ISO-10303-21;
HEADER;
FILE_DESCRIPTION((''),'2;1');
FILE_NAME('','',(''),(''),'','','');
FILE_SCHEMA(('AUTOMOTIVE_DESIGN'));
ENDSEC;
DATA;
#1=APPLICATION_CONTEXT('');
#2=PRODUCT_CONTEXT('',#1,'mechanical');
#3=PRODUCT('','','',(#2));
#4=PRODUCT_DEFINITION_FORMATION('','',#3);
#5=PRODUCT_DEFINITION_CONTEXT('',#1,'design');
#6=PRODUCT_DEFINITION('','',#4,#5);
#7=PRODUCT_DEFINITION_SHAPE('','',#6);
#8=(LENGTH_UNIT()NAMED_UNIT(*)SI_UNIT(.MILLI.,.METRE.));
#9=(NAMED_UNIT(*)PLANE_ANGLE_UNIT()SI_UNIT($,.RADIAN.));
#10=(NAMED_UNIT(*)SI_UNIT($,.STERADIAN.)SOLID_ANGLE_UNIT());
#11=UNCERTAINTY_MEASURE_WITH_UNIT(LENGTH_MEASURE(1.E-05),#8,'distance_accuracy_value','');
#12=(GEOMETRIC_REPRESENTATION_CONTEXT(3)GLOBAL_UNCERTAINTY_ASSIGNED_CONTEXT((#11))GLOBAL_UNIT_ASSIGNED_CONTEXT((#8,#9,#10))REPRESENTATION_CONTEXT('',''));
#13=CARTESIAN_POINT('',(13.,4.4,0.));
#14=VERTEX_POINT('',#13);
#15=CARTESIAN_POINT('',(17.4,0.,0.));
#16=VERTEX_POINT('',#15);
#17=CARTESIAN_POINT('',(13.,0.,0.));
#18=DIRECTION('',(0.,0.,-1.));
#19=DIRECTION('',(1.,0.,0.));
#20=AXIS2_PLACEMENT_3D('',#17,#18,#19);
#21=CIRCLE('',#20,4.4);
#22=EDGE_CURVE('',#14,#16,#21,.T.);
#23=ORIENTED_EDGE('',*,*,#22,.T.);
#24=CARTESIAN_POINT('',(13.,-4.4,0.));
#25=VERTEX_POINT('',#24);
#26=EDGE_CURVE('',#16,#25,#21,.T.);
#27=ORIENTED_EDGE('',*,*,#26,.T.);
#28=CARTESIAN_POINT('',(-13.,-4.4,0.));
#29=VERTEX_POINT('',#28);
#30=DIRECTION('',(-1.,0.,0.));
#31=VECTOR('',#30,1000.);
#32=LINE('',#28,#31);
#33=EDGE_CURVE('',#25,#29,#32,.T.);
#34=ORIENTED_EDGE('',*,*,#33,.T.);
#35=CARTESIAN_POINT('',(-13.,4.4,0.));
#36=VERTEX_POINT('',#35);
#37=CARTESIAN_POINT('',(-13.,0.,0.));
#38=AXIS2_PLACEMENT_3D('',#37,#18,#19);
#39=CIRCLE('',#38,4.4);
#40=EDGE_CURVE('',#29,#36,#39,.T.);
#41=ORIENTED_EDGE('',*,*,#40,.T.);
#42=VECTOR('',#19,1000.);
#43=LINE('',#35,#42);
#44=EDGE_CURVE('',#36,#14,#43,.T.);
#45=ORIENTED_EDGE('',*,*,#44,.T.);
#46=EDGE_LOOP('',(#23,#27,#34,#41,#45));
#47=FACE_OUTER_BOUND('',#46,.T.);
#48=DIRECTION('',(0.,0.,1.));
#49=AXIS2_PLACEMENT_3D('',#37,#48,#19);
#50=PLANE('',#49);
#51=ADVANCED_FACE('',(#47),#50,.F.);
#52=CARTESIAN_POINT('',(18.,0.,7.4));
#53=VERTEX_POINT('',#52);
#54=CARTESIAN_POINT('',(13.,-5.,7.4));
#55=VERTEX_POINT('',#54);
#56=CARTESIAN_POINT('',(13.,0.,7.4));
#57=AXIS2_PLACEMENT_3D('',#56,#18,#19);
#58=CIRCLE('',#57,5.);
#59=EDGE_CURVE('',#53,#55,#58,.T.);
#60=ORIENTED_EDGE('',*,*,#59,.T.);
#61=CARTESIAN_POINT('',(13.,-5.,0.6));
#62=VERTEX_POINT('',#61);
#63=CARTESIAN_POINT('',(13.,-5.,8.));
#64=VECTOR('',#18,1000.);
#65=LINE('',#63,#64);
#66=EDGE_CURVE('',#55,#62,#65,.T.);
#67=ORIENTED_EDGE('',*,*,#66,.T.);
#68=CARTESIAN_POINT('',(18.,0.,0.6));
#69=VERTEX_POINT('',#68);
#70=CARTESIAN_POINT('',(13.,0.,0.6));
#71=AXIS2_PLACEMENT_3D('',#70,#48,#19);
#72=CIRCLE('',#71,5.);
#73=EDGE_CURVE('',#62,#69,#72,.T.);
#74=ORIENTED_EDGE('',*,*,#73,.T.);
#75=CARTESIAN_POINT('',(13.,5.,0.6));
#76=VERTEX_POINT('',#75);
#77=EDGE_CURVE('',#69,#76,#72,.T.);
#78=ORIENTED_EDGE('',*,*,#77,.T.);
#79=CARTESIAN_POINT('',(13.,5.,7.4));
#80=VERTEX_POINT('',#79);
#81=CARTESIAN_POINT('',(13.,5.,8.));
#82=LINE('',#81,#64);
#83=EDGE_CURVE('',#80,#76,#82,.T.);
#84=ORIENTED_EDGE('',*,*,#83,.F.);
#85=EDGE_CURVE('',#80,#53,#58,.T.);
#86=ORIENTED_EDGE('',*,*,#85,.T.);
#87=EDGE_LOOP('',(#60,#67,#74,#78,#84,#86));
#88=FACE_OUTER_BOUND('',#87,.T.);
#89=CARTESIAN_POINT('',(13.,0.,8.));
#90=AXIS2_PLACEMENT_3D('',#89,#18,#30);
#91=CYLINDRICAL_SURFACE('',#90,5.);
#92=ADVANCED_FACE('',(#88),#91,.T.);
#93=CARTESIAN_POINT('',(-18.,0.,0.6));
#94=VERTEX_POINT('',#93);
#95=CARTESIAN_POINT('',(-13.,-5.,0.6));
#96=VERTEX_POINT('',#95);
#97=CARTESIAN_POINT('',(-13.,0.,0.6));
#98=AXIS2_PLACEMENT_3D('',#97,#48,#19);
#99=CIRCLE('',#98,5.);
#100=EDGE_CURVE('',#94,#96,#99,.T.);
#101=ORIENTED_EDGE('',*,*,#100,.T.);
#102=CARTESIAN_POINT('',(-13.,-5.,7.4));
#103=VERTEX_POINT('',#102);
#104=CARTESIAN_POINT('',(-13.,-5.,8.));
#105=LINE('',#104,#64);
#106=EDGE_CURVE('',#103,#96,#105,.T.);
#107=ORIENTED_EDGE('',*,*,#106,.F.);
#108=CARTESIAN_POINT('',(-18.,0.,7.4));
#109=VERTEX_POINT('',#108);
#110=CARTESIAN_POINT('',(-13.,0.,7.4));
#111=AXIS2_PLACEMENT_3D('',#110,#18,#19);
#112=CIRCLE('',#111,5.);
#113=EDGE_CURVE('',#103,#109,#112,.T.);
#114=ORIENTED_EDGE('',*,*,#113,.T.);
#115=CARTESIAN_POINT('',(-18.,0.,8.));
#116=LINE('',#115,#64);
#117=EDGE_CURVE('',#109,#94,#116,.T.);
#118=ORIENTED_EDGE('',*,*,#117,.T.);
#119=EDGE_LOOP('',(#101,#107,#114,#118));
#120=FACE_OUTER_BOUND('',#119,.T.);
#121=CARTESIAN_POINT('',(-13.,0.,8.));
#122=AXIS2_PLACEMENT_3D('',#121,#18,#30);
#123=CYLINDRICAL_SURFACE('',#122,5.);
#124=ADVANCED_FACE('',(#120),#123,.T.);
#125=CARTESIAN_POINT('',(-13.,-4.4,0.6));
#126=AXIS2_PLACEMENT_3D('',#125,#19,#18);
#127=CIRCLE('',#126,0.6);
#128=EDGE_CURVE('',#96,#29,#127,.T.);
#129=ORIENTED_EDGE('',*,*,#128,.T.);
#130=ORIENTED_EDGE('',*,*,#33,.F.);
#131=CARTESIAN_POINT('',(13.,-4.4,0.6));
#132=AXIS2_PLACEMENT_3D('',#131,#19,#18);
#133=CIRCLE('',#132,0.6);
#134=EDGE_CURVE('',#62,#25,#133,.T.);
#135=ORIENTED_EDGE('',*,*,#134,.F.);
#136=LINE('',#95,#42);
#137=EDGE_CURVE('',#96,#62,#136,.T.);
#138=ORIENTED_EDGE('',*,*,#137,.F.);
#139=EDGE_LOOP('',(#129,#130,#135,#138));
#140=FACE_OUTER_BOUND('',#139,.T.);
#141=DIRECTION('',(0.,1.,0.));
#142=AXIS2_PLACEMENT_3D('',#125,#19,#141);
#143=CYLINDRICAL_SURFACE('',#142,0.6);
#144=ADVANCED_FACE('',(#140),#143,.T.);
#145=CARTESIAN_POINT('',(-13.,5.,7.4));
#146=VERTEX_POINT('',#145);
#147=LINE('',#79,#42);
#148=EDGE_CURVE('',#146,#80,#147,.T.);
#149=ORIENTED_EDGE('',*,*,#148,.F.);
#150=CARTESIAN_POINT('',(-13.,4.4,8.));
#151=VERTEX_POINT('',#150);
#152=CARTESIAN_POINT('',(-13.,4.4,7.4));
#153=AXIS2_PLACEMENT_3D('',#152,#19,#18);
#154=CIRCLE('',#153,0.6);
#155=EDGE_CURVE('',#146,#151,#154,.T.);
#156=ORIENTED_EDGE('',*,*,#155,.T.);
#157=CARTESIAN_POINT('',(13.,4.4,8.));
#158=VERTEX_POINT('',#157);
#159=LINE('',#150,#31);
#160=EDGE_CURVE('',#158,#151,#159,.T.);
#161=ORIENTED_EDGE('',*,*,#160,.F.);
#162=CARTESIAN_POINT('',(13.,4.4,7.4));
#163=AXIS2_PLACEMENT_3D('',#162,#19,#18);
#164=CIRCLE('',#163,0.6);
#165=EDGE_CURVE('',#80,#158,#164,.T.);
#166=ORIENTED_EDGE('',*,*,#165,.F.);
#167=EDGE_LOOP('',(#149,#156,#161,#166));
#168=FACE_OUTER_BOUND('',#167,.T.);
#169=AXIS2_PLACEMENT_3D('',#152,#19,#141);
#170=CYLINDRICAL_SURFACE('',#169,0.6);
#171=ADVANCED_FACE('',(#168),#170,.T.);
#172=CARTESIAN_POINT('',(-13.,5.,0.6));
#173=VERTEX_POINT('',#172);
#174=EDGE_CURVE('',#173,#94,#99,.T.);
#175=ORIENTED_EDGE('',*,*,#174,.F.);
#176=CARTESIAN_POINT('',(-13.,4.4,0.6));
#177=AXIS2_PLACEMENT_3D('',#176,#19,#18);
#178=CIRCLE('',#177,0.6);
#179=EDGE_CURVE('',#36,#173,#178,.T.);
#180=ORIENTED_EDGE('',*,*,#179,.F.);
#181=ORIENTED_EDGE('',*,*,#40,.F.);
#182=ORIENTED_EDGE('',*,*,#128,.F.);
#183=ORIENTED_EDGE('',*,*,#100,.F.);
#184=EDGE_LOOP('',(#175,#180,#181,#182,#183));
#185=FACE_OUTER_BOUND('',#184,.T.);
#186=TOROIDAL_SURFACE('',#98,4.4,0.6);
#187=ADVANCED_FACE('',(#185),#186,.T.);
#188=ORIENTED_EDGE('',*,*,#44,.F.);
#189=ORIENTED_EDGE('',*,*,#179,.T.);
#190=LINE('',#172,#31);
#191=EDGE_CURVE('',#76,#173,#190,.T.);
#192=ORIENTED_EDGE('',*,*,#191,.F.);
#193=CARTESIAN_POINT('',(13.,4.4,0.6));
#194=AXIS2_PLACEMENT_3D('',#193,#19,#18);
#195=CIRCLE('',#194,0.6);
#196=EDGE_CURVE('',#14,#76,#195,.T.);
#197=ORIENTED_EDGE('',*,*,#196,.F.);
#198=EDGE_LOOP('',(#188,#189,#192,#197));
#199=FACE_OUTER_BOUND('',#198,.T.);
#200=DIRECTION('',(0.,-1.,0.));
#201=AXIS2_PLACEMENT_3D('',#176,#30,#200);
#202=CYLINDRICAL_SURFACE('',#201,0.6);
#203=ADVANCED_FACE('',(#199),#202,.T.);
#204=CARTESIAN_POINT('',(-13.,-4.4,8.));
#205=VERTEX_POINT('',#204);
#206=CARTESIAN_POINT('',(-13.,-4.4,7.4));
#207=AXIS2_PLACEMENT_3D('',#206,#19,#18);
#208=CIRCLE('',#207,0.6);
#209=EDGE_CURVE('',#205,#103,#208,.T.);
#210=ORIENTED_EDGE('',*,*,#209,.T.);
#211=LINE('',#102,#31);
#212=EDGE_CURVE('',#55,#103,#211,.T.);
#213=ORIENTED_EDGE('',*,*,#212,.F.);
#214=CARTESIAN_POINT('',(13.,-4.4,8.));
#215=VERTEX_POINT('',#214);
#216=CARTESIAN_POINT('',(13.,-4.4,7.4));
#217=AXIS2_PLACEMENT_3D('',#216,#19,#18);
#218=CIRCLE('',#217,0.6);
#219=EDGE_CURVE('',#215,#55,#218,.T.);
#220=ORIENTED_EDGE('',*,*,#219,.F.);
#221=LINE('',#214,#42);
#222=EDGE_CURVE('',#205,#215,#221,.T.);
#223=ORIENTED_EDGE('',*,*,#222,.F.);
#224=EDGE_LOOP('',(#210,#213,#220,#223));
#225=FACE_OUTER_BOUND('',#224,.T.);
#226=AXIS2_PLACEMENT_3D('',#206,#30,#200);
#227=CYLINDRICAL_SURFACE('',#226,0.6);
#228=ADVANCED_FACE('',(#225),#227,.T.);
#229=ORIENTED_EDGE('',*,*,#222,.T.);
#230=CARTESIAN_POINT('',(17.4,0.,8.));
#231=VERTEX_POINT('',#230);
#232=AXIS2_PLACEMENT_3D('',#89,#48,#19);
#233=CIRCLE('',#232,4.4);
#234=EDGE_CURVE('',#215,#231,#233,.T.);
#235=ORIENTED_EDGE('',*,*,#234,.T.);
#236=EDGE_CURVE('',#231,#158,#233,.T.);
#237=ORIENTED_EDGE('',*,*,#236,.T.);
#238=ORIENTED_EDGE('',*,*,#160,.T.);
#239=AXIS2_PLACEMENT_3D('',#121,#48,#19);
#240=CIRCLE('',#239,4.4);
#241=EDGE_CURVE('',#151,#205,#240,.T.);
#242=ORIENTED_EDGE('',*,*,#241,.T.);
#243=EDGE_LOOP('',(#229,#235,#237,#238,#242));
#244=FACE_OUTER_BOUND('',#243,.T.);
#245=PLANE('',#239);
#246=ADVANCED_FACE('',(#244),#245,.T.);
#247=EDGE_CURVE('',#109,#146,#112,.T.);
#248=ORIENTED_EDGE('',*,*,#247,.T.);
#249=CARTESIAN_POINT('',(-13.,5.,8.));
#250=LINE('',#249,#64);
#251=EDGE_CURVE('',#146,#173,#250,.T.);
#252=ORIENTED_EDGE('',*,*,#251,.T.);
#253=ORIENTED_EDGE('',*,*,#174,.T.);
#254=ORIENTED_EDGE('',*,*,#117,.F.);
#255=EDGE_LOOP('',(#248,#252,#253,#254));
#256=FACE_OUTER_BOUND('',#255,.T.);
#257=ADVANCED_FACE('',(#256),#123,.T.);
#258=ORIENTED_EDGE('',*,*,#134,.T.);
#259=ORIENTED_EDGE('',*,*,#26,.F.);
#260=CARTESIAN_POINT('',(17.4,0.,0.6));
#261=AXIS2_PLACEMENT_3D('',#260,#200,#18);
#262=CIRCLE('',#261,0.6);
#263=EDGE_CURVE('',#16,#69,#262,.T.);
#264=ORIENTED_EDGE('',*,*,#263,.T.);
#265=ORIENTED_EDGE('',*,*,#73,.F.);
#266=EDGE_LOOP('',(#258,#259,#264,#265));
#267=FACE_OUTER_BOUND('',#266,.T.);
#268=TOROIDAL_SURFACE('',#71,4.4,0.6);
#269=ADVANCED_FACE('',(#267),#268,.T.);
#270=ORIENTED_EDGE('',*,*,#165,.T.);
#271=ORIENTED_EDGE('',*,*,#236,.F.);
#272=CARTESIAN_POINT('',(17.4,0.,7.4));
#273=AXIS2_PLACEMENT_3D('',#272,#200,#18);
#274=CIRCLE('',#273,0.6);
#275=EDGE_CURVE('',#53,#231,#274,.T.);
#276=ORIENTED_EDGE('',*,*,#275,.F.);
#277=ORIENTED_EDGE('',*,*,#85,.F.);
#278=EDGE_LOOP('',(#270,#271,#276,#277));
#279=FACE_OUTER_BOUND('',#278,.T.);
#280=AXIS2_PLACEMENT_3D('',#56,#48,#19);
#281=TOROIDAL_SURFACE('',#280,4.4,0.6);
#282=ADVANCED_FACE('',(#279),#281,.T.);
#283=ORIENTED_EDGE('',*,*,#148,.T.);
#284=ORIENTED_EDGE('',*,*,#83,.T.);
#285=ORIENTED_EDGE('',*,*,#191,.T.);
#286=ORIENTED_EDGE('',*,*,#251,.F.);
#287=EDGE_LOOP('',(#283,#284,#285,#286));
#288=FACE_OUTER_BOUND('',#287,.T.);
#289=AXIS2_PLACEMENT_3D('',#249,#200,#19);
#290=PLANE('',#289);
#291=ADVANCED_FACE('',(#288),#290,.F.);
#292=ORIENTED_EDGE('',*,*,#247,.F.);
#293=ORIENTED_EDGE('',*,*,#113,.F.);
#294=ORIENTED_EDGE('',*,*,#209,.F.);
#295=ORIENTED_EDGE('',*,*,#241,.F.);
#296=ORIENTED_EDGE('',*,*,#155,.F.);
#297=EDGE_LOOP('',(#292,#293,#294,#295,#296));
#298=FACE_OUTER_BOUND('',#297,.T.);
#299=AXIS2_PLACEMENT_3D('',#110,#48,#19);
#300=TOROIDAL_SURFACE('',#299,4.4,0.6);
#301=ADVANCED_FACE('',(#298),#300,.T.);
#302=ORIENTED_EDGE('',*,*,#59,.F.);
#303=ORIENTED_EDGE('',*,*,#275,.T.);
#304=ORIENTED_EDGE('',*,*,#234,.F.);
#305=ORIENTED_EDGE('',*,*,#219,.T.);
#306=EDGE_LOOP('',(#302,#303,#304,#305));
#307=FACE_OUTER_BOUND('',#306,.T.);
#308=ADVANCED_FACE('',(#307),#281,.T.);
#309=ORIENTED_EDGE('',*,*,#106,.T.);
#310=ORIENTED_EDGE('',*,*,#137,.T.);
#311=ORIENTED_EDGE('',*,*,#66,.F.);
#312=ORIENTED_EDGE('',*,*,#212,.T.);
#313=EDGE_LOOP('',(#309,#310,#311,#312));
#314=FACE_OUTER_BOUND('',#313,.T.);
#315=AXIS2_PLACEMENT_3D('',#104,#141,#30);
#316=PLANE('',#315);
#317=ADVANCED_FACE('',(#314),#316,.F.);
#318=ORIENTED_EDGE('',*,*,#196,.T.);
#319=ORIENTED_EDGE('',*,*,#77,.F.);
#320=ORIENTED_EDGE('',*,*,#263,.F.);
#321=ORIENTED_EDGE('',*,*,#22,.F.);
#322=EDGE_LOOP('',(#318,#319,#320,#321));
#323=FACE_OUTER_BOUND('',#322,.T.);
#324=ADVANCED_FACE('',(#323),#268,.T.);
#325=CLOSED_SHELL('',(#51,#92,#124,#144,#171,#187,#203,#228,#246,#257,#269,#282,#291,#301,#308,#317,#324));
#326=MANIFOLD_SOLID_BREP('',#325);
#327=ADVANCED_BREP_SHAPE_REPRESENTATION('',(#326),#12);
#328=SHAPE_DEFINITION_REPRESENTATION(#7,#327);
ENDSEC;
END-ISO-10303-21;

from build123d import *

# Parameters (mm, degrees)
EXTRUDE_512_DEPTH = 8
FILLET_1_R        = 0.6


with BuildPart() as part:
    # 草图1 → Extrude 512 (new body)
    with BuildSketch(Plane.XY):
        with BuildLine():
            Line((-13, 5), (13, 5))
            ThreePointArc((13, 5), (18, 0), (13, -5))
            Line((13, -5), (-13, -5))
            ThreePointArc((-13, -5), (-18, 0), (-13, 5))
        make_face()
    extrude(amount=EXTRUDE_512_DEPTH)

    # 圆角1
    fillet_1_edges = [part.edges().sort_by_distance(p)[0] for p in [
        (18, 0, 8),
        (0, 5, 8),
        (-18, 0, 8),
        (0, 5, 0),
        (18, 0, 0),
        (0, -5, 0),
        (-18, 0, 0),
        (0, -5, 8),
    ]]
    fillet(fillet_1_edges, radius=FILLET_1_R)


solid = part.part
